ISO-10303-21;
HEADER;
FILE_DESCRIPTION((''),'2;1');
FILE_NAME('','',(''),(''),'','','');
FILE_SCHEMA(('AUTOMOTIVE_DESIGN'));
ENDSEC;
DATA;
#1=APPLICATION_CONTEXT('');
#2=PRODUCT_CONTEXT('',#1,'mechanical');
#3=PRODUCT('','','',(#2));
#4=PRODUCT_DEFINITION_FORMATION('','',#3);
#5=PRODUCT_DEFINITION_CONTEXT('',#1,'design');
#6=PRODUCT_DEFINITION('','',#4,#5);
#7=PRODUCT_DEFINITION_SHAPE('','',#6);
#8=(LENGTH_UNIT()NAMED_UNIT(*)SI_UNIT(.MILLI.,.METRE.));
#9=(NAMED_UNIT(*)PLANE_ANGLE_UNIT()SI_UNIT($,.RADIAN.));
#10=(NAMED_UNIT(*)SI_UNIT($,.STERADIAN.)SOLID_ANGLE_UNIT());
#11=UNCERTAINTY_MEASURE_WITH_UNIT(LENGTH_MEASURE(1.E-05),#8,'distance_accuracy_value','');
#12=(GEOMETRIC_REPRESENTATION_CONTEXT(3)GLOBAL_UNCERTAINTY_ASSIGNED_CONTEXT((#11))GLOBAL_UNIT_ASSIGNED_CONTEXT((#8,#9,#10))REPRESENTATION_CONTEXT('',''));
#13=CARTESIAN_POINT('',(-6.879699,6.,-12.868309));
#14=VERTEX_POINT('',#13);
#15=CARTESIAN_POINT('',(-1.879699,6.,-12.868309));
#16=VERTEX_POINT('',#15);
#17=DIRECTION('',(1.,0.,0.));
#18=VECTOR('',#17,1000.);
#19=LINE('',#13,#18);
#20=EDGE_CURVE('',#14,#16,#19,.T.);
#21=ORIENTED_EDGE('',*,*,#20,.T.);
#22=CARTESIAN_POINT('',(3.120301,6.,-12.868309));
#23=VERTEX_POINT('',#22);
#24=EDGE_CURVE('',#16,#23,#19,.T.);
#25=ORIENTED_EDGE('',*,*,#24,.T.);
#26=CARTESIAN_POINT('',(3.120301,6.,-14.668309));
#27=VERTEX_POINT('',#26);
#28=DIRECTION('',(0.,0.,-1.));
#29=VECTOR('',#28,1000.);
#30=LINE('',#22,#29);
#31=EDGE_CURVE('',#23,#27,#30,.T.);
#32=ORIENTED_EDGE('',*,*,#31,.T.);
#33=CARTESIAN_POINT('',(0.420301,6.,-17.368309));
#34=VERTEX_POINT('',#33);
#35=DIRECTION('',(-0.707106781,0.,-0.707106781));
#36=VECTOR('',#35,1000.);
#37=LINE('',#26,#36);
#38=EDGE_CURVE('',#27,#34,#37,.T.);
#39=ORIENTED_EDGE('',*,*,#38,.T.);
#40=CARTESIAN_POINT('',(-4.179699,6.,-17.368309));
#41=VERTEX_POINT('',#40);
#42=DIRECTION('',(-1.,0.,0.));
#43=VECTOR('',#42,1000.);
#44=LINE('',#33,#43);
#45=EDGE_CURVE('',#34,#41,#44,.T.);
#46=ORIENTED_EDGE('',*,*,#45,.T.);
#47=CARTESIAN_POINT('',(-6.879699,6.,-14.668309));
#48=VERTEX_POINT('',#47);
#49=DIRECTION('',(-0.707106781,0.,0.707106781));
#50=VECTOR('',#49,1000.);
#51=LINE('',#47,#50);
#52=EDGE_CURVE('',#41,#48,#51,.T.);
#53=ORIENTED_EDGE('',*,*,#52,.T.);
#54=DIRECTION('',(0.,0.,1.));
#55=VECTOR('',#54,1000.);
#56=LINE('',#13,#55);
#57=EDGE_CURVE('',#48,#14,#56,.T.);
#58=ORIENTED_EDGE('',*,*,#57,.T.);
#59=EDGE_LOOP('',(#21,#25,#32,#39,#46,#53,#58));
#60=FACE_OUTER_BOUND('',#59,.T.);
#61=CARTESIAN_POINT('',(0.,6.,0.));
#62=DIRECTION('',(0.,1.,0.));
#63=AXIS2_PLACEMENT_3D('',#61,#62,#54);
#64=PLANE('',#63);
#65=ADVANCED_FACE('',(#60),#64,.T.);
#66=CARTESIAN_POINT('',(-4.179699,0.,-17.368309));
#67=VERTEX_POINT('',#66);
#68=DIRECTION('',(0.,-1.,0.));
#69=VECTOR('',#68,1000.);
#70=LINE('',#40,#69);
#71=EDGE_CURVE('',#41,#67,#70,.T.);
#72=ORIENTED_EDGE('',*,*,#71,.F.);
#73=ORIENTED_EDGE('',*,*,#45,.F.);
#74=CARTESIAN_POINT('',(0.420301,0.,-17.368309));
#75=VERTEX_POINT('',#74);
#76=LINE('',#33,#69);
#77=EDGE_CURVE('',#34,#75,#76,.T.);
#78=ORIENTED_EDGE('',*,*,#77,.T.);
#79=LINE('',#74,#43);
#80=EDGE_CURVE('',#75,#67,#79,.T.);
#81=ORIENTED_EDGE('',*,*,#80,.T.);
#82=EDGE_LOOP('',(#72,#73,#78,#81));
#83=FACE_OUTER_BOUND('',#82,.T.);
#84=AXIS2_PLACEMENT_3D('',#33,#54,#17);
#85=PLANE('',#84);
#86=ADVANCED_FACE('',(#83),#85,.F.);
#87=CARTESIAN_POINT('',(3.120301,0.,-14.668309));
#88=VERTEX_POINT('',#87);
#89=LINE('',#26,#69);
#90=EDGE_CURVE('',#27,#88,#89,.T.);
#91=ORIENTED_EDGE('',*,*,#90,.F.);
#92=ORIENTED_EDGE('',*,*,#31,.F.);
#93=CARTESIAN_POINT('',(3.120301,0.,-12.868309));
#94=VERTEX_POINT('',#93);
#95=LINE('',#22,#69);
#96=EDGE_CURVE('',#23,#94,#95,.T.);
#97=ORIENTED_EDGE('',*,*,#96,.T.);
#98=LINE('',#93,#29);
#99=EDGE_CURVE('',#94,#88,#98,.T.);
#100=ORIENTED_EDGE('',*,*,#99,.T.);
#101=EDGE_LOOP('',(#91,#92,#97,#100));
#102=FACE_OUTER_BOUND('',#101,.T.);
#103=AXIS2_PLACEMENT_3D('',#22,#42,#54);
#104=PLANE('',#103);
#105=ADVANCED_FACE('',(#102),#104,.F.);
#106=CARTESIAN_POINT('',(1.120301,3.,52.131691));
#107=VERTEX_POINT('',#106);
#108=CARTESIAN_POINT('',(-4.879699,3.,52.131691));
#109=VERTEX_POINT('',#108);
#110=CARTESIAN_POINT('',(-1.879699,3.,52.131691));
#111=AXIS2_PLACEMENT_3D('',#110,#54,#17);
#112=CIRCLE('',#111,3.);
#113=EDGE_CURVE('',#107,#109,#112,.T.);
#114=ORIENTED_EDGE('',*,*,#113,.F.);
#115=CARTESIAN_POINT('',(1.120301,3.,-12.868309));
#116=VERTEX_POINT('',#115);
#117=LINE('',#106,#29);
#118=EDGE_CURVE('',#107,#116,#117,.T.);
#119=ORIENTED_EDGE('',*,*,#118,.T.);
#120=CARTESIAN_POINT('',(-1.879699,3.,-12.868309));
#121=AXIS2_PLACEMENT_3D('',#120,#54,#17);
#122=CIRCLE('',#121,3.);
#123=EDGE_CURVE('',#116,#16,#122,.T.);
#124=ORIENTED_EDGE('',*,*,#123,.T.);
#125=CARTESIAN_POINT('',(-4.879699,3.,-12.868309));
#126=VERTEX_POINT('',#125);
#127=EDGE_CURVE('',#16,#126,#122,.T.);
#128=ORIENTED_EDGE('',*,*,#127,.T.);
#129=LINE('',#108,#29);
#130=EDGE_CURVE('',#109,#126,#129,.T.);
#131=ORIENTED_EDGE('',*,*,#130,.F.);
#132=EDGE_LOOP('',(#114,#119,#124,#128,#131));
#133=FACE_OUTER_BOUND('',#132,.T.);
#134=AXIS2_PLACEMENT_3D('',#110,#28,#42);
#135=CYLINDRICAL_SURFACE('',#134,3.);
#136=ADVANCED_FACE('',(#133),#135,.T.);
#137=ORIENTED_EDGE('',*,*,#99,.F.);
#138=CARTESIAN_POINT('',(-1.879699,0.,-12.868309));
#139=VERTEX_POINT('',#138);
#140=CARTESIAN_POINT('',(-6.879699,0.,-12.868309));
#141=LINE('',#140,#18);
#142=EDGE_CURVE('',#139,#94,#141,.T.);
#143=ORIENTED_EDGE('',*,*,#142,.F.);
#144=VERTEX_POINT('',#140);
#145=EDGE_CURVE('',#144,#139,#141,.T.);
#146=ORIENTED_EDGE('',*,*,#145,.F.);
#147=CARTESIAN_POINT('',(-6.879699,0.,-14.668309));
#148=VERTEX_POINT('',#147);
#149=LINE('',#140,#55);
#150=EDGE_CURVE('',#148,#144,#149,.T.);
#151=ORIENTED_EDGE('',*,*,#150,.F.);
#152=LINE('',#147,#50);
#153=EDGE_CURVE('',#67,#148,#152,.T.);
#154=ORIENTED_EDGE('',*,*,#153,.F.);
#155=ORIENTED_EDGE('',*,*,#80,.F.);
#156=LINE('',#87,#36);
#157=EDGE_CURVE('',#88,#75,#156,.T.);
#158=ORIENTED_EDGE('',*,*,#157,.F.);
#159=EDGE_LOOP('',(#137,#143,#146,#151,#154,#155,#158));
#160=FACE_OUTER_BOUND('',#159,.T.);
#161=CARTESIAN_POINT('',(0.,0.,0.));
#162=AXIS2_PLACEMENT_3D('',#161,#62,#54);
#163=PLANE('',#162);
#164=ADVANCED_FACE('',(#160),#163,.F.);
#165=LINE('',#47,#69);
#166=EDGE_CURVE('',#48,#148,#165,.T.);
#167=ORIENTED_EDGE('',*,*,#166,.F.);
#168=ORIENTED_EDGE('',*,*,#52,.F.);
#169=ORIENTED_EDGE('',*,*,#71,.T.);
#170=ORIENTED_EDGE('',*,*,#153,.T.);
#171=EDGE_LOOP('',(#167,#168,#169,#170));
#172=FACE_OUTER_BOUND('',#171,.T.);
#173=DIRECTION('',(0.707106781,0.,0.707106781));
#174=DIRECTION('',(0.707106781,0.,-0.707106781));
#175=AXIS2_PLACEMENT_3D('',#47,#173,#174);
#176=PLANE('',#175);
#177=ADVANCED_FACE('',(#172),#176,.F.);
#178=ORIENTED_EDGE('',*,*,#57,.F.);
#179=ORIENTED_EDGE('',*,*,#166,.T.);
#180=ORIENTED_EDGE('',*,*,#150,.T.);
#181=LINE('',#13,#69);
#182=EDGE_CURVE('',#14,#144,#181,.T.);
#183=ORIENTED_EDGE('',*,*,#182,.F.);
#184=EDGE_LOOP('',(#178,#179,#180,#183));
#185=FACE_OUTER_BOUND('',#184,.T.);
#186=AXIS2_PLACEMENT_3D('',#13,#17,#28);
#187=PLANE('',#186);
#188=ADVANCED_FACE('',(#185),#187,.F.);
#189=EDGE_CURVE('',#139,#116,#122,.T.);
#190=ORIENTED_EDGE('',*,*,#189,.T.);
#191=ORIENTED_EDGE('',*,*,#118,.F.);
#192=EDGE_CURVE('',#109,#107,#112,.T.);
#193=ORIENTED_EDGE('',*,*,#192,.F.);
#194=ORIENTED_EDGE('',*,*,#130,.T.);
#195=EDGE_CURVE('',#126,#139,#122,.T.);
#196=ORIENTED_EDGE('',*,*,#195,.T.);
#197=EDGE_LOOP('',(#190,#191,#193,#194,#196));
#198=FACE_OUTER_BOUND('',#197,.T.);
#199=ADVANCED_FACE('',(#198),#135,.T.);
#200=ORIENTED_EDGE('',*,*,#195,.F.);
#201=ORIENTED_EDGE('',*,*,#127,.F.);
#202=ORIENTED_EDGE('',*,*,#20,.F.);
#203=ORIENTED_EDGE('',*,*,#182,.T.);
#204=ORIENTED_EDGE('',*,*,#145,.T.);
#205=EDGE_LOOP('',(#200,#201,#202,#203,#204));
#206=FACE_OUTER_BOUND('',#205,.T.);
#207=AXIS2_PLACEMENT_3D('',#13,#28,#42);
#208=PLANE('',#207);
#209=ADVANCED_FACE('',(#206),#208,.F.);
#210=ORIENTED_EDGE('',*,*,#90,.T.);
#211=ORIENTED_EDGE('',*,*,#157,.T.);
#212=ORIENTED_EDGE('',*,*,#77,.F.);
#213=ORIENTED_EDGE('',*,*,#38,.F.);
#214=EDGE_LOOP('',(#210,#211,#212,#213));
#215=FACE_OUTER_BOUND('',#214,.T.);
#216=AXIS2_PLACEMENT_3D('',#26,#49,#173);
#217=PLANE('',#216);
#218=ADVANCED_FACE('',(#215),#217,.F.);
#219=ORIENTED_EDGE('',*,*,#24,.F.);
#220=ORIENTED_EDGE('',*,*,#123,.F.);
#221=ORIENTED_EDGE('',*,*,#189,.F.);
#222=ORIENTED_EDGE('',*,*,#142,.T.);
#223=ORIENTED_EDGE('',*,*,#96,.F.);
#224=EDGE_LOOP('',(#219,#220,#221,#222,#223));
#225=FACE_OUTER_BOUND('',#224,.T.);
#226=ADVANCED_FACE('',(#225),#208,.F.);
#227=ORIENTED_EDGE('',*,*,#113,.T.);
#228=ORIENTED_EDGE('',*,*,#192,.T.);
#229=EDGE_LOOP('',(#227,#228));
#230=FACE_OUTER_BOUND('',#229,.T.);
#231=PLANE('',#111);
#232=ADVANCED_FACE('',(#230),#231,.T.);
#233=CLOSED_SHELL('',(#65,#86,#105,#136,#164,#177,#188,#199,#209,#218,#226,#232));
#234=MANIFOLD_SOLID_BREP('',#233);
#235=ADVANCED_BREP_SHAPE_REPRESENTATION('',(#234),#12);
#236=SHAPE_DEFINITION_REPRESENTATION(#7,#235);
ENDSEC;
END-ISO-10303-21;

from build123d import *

# Parameters (mm, degrees)
BOSS_EXTRUDE1_DEPTH = 6
SKETCH2_R           = 3
BOSS_EXTRUDE2_DEPTH = 65


with BuildPart() as part:
    # Sketch1 → Boss-Extrude1 (new body)
    with BuildSketch(Plane(origin=(0, 0, 0), x_dir=(1, 0, 0), z_dir=(0, 1, 0))):
        Polygon((-6.879699248, 12.868308957), (3.120300752, 12.868308957), (3.120300752, 14.668308957), (0.420300752, 17.368308957), (-4.179699248, 17.368308957), (-6.879699248, 14.668308957), align=None)
    extrude(amount=BOSS_EXTRUDE1_DEPTH)

    # Sketch2 → Boss-Extrude2 (add)
    with BuildSketch(Plane.XY.offset(-12.868308957)):
        with Locations(Location((-1.879699248, 3, 0), (0, 0, 270))):
            Circle(SKETCH2_R)
    extrude(amount=BOSS_EXTRUDE2_DEPTH)


solid = part.part
